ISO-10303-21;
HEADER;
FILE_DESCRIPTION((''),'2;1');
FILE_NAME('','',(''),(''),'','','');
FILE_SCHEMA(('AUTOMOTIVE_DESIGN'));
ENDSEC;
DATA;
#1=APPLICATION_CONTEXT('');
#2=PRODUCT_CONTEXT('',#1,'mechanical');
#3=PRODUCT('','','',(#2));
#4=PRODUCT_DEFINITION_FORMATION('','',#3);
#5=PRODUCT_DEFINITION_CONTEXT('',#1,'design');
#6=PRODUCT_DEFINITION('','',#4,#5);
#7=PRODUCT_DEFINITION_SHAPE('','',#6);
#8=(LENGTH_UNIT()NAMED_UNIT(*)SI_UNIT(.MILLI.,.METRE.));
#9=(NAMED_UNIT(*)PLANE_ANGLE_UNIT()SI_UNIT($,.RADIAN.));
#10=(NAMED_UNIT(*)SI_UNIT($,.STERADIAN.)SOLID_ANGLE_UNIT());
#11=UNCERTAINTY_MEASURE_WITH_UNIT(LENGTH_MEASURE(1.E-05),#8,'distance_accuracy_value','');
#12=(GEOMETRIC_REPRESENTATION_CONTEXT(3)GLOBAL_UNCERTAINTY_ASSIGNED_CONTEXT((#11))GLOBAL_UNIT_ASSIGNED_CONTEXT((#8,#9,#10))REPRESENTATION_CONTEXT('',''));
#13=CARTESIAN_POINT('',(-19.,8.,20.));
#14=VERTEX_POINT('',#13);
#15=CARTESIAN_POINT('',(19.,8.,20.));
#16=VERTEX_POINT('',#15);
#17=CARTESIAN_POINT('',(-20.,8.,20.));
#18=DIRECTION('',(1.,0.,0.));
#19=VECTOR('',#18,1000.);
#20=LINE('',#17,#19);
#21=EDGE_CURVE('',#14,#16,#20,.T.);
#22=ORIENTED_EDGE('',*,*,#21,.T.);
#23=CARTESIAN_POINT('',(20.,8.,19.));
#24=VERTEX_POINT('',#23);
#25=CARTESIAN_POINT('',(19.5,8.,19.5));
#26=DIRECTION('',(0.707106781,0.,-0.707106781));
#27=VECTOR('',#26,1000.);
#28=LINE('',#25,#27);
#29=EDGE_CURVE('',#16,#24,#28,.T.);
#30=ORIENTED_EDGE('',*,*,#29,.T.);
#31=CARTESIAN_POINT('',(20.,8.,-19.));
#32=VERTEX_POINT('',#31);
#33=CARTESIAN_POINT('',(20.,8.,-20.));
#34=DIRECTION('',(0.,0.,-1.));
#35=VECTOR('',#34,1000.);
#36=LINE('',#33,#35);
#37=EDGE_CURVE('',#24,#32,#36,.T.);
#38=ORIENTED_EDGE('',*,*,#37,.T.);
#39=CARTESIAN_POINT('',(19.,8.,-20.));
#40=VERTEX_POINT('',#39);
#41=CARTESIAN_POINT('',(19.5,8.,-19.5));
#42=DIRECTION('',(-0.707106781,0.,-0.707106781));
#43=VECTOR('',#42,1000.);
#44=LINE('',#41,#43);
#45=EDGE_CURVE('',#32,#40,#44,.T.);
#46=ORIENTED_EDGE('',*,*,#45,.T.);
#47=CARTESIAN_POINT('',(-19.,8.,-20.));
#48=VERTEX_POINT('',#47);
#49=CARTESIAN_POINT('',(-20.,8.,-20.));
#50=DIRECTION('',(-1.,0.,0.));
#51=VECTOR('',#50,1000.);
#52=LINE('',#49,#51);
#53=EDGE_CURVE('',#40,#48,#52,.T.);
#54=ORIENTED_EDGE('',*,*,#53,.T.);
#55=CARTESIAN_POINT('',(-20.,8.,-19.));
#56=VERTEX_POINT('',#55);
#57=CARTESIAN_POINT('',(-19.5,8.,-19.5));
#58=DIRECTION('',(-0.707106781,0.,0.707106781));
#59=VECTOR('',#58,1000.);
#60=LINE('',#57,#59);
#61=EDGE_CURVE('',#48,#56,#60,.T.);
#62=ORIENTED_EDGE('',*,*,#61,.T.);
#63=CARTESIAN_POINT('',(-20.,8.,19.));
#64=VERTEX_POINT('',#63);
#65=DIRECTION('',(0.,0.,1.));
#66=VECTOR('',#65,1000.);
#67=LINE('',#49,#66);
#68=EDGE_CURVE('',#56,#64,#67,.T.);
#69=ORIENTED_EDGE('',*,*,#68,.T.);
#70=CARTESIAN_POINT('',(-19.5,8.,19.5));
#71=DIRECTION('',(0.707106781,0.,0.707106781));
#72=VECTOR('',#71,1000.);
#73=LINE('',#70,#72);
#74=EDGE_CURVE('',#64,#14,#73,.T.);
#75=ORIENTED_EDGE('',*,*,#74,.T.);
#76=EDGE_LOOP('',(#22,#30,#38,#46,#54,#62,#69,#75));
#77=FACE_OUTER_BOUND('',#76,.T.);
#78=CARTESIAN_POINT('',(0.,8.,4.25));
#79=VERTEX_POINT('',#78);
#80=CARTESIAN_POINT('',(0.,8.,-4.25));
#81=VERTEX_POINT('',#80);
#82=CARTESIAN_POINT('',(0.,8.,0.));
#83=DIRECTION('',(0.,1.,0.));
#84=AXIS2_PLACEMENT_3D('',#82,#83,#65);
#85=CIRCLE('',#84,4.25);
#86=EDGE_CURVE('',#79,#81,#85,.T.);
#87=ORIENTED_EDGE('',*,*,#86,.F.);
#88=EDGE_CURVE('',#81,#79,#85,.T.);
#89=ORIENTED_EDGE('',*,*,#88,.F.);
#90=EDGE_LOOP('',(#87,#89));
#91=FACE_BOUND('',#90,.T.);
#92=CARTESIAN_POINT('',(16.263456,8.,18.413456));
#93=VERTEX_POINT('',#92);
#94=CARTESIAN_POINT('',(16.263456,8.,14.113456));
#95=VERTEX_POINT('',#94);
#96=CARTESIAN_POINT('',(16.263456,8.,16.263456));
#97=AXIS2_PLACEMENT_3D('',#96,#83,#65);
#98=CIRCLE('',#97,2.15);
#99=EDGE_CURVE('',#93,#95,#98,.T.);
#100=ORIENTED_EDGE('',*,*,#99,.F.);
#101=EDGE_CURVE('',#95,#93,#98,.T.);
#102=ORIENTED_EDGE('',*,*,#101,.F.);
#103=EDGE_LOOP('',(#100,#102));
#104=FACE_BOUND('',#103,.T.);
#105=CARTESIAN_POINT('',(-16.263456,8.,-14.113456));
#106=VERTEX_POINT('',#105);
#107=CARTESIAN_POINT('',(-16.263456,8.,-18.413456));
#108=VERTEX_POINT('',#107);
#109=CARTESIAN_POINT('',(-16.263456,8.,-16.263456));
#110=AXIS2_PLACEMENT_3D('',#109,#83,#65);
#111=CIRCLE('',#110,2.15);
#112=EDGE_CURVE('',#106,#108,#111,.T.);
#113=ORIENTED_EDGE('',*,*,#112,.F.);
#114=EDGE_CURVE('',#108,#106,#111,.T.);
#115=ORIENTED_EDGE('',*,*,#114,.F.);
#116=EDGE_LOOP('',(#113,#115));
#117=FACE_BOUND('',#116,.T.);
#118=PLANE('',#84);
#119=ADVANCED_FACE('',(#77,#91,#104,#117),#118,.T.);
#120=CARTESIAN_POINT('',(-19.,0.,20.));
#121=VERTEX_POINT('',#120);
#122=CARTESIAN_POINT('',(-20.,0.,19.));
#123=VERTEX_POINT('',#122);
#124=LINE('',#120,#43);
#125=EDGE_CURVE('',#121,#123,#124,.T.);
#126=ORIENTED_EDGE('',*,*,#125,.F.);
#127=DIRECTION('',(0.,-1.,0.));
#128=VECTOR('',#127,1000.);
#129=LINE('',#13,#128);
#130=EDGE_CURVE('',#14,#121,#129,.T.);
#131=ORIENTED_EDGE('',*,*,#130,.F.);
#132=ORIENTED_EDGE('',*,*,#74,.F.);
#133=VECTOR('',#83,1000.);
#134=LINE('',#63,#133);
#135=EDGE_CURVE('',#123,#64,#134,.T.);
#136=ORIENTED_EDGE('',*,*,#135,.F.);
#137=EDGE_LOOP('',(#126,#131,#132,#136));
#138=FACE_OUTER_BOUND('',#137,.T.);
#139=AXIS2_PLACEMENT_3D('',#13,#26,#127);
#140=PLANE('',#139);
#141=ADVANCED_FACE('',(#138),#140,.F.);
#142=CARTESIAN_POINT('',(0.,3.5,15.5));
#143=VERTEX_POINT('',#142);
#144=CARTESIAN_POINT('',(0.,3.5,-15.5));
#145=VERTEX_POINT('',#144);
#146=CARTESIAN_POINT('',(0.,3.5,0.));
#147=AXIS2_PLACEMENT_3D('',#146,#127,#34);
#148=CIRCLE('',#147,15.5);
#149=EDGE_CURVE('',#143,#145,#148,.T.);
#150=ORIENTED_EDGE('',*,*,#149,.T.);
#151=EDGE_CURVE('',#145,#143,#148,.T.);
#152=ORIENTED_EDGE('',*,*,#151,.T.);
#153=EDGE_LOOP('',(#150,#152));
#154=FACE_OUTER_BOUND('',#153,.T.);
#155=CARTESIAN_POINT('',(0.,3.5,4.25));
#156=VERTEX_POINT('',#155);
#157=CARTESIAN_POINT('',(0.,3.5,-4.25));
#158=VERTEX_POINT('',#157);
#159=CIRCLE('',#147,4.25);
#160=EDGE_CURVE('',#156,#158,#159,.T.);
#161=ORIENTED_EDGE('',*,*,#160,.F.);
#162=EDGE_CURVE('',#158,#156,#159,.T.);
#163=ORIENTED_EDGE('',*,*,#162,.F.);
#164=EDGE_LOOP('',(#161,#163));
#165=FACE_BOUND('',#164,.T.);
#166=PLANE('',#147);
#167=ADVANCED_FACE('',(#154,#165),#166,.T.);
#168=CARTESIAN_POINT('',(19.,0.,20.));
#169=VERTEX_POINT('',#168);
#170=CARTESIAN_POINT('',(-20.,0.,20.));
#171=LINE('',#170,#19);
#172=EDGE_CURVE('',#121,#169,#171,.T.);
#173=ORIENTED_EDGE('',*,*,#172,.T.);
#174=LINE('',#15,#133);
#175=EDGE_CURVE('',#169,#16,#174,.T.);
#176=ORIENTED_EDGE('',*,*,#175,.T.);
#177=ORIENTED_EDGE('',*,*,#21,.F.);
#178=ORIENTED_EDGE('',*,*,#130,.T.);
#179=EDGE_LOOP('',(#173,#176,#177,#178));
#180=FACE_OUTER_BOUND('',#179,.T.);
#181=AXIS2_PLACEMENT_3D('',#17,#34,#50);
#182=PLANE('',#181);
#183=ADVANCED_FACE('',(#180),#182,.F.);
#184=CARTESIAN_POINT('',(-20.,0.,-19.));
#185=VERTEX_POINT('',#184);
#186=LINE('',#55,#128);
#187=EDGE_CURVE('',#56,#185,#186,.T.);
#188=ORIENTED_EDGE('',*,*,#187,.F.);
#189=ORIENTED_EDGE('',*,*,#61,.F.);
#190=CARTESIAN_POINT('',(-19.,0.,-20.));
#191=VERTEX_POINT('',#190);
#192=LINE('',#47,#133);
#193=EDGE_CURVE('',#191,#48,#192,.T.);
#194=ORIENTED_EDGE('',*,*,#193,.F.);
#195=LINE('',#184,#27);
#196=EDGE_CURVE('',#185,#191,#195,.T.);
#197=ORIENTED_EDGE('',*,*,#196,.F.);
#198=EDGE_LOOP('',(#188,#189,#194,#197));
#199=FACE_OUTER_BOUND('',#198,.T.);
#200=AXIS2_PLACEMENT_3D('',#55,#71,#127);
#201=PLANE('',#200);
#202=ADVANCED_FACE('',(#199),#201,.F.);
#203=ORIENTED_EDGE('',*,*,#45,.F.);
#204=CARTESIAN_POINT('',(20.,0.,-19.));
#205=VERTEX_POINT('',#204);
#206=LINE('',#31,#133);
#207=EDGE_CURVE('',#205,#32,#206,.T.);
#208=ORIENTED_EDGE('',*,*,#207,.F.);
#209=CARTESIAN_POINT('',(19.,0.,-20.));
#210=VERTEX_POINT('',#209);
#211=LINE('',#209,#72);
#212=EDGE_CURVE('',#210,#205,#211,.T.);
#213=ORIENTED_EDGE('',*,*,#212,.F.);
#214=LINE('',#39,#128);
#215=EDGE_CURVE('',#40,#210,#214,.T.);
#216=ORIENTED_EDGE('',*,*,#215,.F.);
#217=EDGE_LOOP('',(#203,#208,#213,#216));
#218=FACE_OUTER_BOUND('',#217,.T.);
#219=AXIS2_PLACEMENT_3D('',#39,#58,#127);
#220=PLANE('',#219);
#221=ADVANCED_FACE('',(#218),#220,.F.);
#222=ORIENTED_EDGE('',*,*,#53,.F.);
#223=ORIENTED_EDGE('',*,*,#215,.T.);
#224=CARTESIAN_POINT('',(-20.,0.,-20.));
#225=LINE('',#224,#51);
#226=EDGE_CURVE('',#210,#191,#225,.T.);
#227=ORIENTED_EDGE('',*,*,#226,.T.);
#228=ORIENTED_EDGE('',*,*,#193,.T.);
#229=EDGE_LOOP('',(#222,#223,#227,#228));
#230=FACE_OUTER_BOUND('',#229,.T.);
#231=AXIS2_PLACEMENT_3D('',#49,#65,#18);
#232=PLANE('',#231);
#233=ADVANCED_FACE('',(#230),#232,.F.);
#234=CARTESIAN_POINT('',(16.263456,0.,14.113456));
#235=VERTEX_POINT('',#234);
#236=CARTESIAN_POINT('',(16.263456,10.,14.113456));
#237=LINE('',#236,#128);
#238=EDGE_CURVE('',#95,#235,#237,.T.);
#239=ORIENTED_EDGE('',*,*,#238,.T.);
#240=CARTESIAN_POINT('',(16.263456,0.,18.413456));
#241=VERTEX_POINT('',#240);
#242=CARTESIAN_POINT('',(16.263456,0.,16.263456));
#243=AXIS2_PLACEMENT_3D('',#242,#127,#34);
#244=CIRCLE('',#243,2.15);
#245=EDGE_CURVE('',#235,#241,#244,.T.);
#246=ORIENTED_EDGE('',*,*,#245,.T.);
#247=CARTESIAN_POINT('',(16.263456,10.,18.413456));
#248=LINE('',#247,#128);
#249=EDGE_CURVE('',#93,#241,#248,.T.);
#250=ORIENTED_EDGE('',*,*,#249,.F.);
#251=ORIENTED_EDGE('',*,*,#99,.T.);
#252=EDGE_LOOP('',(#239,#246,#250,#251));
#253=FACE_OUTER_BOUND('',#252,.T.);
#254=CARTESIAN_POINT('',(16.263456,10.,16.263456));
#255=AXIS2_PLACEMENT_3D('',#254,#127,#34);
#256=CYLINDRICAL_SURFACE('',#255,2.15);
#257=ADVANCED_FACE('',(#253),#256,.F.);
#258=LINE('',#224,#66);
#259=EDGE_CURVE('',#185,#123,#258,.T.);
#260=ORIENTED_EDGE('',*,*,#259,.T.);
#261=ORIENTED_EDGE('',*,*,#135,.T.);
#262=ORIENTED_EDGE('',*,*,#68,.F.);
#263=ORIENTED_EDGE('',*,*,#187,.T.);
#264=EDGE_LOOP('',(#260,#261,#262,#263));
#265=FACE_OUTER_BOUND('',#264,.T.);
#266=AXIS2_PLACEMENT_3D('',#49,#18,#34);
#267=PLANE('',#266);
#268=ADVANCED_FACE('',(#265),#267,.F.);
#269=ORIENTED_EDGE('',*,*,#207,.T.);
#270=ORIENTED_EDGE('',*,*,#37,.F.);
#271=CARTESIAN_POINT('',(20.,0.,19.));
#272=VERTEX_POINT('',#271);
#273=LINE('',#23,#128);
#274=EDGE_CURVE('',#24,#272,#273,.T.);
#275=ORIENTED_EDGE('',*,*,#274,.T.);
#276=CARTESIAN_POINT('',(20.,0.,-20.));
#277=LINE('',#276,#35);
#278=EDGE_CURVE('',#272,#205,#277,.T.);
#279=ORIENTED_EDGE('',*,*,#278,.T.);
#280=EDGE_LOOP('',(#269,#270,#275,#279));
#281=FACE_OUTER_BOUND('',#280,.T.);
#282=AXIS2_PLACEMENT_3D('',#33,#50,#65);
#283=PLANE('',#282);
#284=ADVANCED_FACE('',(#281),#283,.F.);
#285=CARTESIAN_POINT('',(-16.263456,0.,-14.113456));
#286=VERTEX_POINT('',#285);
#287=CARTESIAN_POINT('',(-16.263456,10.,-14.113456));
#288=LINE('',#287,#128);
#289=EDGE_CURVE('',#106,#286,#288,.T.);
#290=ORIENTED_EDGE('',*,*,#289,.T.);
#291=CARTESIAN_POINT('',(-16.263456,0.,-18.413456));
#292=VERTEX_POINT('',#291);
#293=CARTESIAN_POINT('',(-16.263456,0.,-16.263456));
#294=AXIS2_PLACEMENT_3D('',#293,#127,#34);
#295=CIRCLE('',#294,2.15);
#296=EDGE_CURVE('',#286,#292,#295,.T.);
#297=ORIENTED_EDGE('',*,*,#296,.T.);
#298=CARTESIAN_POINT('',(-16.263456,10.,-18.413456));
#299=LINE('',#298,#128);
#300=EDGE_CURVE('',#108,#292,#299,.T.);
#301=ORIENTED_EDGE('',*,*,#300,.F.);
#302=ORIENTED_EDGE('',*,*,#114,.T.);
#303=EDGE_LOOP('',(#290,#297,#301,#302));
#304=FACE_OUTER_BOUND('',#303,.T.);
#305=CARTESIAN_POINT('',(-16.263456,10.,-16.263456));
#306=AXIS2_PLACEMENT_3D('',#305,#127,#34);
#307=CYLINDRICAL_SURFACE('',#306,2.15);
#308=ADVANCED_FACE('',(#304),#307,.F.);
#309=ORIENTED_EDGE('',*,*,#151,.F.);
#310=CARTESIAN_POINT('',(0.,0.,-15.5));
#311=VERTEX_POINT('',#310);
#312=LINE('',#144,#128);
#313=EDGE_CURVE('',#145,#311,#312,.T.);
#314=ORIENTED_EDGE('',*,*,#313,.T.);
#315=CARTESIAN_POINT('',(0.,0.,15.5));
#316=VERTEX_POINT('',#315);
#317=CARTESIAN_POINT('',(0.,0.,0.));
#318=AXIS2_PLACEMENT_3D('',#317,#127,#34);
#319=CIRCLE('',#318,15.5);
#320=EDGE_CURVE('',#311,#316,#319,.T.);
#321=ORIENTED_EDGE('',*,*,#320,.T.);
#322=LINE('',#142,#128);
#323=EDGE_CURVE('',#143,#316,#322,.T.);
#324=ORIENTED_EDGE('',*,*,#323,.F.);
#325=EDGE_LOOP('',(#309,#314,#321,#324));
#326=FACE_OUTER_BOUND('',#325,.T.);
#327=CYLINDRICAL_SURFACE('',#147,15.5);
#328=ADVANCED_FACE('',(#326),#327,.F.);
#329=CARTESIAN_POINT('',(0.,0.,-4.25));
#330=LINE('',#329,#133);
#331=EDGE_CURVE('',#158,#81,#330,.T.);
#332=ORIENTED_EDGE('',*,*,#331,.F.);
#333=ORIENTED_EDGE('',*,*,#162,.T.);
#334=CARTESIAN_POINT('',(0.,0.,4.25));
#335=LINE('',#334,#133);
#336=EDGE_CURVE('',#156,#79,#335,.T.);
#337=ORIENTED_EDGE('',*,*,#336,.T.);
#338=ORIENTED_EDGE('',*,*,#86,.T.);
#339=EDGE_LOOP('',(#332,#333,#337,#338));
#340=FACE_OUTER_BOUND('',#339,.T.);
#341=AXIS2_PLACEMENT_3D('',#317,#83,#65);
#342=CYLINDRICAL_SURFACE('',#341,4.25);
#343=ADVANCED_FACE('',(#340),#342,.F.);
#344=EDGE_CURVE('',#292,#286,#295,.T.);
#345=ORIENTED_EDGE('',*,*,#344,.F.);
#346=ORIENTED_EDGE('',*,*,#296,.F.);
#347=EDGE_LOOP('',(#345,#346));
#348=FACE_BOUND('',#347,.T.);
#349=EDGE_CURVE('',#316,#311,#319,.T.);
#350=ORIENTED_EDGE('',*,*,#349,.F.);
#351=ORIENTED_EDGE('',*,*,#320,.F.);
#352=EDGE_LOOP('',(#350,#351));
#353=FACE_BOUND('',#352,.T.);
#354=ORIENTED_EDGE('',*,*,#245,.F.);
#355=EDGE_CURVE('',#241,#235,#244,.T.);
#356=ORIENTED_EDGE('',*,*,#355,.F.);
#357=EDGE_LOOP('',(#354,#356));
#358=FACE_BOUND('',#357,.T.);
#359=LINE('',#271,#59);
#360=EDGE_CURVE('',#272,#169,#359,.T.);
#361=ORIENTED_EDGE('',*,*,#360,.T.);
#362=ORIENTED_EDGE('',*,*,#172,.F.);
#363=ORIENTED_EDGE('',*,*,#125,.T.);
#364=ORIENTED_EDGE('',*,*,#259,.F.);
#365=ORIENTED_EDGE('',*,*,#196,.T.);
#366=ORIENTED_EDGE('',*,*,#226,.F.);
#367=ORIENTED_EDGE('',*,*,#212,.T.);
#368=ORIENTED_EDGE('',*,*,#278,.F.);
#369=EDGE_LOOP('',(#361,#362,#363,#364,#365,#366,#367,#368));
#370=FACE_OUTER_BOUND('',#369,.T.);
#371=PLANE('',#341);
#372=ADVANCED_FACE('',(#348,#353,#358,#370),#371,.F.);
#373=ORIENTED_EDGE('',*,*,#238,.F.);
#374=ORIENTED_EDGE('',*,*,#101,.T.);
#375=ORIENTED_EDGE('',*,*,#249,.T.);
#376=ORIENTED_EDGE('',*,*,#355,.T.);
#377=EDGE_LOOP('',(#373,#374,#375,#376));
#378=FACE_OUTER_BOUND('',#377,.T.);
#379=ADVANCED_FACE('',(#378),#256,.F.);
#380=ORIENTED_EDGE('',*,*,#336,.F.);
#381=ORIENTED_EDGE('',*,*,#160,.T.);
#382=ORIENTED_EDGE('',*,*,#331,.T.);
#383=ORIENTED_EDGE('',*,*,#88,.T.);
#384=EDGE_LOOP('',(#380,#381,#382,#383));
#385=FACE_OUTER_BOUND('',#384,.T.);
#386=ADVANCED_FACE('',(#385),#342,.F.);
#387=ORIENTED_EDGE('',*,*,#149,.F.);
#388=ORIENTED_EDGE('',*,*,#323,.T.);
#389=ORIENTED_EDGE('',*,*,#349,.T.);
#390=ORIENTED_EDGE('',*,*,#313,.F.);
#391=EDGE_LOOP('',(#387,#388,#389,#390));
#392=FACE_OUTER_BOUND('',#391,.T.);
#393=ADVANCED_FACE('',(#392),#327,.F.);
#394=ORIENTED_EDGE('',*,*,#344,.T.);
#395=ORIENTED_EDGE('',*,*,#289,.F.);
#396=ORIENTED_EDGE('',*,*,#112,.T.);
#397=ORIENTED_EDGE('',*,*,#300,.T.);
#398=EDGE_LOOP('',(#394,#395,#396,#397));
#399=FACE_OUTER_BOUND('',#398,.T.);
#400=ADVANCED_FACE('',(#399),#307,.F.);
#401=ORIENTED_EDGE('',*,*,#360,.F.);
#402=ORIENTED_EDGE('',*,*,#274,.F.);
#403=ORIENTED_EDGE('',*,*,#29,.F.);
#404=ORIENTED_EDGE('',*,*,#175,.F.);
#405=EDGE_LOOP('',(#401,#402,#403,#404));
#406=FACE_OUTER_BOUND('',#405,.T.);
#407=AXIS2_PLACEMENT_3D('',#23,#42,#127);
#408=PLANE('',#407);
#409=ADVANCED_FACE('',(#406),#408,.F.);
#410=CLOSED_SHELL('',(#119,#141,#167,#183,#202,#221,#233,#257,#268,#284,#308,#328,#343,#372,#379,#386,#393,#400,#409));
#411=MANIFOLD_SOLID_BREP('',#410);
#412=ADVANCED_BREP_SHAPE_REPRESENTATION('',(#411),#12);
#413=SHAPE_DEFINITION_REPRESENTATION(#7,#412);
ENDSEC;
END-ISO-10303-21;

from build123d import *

# Parameters (mm, degrees)
SKETCH1_W           = 40
SKETCH1_H           = 40
BOSS_EXTRUDE1_DEPTH = 8
CHAMFER1_SIZE       = 1
SKETCH2_R           = 15.5
CUT_EXTRUDE1_DEPTH  = 3.5
SKETCH3_R           = 4.25
CUT_EXTRUDE2_DEPTH  = 30.393876913
SKETCH4_R           = 2.15
CUT_EXTRUDE3_DEPTH  = 10


with BuildPart() as part:
    # Sketch1 → Boss-Extrude1 (new body)
    with BuildSketch(Plane(origin=(0, 0, 0), x_dir=(1, 0, 0), z_dir=(0, 1, 0))):
        Rectangle(SKETCH1_W, SKETCH1_H)
    extrude(amount=BOSS_EXTRUDE1_DEPTH)

    # Chamfer1
    chamfer1_edges = [part.edges().sort_by_distance(p)[0] for p in [
        (20, 4, 20),
        (-20, 4, 20),
        (-20, 4, -20),
        (20, 4, -20),
    ]]
    chamfer(chamfer1_edges, length=CHAMFER1_SIZE)

    # Sketch2 → Cut-Extrude1 (cut)
    with BuildSketch(Plane.XZ):
        with Locations(Location((0, 0, 0), (0, 0, 270))):
            Circle(SKETCH2_R)
    extrude(amount=-CUT_EXTRUDE1_DEPTH, mode=Mode.SUBTRACT)

    # Sketch3 → Cut-Extrude2 (cut, through all)
    with BuildSketch(Plane(origin=(0, 8, 0), x_dir=(1, 0, 0), z_dir=(0, 1, 0))):
        with Locations(Location((0, 0, 0), (0, 0, 270))):
            Circle(SKETCH3_R)
    extrude(amount=-CUT_EXTRUDE2_DEPTH, mode=Mode.SUBTRACT)

    # Sketch4 → Cut-Extrude3 (cut)
    with BuildSketch(Plane.XZ):
        with Locations(Location((16.263455967, 16.263455967, 0), (0, 0, 270))):
            Circle(SKETCH4_R)
        with Locations(Location((-16.263455967, -16.263455967, 0), (0, 0, 270))):
            Circle(SKETCH4_R)
    extrude(amount=-CUT_EXTRUDE3_DEPTH, mode=Mode.SUBTRACT)


solid = part.part
